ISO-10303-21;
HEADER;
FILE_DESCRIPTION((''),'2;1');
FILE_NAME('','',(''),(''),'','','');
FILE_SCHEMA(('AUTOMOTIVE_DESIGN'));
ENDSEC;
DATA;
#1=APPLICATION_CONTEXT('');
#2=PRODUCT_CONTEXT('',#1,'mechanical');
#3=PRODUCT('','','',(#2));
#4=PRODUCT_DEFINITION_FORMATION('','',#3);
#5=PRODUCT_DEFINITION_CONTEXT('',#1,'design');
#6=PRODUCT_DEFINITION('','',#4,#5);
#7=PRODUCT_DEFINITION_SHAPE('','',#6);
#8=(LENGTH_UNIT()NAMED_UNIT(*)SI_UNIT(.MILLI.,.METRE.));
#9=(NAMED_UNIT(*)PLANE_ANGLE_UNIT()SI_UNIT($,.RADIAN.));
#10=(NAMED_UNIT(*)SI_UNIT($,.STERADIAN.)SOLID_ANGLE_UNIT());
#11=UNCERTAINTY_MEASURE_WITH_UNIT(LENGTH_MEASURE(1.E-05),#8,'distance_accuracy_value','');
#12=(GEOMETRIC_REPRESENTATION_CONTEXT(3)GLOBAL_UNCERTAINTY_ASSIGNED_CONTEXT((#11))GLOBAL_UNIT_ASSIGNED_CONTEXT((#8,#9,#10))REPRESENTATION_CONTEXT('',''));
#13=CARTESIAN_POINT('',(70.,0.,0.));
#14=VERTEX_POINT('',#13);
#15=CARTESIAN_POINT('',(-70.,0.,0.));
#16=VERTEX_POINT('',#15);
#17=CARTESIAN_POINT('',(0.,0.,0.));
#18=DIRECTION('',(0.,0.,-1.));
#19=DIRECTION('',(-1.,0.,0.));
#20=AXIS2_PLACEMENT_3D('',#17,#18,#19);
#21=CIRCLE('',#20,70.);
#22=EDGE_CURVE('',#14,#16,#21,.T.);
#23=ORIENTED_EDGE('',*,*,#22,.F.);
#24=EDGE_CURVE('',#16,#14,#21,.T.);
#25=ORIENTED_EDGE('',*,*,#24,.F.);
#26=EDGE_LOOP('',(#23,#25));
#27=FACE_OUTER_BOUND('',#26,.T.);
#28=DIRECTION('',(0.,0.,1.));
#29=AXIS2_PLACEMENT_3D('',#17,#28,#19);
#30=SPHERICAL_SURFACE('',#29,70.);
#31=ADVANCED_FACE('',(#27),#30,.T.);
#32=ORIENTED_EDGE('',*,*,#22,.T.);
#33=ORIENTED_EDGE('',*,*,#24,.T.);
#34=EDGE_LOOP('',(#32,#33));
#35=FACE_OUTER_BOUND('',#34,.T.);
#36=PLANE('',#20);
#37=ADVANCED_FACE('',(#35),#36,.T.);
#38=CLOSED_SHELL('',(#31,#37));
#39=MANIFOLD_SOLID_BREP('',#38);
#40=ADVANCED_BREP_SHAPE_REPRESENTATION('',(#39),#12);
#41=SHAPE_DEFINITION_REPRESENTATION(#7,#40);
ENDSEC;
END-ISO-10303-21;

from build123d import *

# Parameters (mm, degrees)
REVOLVE_1_ANGLE = 180


with BuildPart() as part:
    # 草图1 → 旋转1 (revolve)
    with BuildSketch(Plane.XY):
        with BuildLine():
            Line((0, 70), (0, -70))
            ThreePointArc((0, -70), (70, 0), (0, 70))
        make_face()
    revolve(axis=Axis((0, 70, 0), (0, -1, 0)), revolution_arc=REVOLVE_1_ANGLE)


solid = part.part
